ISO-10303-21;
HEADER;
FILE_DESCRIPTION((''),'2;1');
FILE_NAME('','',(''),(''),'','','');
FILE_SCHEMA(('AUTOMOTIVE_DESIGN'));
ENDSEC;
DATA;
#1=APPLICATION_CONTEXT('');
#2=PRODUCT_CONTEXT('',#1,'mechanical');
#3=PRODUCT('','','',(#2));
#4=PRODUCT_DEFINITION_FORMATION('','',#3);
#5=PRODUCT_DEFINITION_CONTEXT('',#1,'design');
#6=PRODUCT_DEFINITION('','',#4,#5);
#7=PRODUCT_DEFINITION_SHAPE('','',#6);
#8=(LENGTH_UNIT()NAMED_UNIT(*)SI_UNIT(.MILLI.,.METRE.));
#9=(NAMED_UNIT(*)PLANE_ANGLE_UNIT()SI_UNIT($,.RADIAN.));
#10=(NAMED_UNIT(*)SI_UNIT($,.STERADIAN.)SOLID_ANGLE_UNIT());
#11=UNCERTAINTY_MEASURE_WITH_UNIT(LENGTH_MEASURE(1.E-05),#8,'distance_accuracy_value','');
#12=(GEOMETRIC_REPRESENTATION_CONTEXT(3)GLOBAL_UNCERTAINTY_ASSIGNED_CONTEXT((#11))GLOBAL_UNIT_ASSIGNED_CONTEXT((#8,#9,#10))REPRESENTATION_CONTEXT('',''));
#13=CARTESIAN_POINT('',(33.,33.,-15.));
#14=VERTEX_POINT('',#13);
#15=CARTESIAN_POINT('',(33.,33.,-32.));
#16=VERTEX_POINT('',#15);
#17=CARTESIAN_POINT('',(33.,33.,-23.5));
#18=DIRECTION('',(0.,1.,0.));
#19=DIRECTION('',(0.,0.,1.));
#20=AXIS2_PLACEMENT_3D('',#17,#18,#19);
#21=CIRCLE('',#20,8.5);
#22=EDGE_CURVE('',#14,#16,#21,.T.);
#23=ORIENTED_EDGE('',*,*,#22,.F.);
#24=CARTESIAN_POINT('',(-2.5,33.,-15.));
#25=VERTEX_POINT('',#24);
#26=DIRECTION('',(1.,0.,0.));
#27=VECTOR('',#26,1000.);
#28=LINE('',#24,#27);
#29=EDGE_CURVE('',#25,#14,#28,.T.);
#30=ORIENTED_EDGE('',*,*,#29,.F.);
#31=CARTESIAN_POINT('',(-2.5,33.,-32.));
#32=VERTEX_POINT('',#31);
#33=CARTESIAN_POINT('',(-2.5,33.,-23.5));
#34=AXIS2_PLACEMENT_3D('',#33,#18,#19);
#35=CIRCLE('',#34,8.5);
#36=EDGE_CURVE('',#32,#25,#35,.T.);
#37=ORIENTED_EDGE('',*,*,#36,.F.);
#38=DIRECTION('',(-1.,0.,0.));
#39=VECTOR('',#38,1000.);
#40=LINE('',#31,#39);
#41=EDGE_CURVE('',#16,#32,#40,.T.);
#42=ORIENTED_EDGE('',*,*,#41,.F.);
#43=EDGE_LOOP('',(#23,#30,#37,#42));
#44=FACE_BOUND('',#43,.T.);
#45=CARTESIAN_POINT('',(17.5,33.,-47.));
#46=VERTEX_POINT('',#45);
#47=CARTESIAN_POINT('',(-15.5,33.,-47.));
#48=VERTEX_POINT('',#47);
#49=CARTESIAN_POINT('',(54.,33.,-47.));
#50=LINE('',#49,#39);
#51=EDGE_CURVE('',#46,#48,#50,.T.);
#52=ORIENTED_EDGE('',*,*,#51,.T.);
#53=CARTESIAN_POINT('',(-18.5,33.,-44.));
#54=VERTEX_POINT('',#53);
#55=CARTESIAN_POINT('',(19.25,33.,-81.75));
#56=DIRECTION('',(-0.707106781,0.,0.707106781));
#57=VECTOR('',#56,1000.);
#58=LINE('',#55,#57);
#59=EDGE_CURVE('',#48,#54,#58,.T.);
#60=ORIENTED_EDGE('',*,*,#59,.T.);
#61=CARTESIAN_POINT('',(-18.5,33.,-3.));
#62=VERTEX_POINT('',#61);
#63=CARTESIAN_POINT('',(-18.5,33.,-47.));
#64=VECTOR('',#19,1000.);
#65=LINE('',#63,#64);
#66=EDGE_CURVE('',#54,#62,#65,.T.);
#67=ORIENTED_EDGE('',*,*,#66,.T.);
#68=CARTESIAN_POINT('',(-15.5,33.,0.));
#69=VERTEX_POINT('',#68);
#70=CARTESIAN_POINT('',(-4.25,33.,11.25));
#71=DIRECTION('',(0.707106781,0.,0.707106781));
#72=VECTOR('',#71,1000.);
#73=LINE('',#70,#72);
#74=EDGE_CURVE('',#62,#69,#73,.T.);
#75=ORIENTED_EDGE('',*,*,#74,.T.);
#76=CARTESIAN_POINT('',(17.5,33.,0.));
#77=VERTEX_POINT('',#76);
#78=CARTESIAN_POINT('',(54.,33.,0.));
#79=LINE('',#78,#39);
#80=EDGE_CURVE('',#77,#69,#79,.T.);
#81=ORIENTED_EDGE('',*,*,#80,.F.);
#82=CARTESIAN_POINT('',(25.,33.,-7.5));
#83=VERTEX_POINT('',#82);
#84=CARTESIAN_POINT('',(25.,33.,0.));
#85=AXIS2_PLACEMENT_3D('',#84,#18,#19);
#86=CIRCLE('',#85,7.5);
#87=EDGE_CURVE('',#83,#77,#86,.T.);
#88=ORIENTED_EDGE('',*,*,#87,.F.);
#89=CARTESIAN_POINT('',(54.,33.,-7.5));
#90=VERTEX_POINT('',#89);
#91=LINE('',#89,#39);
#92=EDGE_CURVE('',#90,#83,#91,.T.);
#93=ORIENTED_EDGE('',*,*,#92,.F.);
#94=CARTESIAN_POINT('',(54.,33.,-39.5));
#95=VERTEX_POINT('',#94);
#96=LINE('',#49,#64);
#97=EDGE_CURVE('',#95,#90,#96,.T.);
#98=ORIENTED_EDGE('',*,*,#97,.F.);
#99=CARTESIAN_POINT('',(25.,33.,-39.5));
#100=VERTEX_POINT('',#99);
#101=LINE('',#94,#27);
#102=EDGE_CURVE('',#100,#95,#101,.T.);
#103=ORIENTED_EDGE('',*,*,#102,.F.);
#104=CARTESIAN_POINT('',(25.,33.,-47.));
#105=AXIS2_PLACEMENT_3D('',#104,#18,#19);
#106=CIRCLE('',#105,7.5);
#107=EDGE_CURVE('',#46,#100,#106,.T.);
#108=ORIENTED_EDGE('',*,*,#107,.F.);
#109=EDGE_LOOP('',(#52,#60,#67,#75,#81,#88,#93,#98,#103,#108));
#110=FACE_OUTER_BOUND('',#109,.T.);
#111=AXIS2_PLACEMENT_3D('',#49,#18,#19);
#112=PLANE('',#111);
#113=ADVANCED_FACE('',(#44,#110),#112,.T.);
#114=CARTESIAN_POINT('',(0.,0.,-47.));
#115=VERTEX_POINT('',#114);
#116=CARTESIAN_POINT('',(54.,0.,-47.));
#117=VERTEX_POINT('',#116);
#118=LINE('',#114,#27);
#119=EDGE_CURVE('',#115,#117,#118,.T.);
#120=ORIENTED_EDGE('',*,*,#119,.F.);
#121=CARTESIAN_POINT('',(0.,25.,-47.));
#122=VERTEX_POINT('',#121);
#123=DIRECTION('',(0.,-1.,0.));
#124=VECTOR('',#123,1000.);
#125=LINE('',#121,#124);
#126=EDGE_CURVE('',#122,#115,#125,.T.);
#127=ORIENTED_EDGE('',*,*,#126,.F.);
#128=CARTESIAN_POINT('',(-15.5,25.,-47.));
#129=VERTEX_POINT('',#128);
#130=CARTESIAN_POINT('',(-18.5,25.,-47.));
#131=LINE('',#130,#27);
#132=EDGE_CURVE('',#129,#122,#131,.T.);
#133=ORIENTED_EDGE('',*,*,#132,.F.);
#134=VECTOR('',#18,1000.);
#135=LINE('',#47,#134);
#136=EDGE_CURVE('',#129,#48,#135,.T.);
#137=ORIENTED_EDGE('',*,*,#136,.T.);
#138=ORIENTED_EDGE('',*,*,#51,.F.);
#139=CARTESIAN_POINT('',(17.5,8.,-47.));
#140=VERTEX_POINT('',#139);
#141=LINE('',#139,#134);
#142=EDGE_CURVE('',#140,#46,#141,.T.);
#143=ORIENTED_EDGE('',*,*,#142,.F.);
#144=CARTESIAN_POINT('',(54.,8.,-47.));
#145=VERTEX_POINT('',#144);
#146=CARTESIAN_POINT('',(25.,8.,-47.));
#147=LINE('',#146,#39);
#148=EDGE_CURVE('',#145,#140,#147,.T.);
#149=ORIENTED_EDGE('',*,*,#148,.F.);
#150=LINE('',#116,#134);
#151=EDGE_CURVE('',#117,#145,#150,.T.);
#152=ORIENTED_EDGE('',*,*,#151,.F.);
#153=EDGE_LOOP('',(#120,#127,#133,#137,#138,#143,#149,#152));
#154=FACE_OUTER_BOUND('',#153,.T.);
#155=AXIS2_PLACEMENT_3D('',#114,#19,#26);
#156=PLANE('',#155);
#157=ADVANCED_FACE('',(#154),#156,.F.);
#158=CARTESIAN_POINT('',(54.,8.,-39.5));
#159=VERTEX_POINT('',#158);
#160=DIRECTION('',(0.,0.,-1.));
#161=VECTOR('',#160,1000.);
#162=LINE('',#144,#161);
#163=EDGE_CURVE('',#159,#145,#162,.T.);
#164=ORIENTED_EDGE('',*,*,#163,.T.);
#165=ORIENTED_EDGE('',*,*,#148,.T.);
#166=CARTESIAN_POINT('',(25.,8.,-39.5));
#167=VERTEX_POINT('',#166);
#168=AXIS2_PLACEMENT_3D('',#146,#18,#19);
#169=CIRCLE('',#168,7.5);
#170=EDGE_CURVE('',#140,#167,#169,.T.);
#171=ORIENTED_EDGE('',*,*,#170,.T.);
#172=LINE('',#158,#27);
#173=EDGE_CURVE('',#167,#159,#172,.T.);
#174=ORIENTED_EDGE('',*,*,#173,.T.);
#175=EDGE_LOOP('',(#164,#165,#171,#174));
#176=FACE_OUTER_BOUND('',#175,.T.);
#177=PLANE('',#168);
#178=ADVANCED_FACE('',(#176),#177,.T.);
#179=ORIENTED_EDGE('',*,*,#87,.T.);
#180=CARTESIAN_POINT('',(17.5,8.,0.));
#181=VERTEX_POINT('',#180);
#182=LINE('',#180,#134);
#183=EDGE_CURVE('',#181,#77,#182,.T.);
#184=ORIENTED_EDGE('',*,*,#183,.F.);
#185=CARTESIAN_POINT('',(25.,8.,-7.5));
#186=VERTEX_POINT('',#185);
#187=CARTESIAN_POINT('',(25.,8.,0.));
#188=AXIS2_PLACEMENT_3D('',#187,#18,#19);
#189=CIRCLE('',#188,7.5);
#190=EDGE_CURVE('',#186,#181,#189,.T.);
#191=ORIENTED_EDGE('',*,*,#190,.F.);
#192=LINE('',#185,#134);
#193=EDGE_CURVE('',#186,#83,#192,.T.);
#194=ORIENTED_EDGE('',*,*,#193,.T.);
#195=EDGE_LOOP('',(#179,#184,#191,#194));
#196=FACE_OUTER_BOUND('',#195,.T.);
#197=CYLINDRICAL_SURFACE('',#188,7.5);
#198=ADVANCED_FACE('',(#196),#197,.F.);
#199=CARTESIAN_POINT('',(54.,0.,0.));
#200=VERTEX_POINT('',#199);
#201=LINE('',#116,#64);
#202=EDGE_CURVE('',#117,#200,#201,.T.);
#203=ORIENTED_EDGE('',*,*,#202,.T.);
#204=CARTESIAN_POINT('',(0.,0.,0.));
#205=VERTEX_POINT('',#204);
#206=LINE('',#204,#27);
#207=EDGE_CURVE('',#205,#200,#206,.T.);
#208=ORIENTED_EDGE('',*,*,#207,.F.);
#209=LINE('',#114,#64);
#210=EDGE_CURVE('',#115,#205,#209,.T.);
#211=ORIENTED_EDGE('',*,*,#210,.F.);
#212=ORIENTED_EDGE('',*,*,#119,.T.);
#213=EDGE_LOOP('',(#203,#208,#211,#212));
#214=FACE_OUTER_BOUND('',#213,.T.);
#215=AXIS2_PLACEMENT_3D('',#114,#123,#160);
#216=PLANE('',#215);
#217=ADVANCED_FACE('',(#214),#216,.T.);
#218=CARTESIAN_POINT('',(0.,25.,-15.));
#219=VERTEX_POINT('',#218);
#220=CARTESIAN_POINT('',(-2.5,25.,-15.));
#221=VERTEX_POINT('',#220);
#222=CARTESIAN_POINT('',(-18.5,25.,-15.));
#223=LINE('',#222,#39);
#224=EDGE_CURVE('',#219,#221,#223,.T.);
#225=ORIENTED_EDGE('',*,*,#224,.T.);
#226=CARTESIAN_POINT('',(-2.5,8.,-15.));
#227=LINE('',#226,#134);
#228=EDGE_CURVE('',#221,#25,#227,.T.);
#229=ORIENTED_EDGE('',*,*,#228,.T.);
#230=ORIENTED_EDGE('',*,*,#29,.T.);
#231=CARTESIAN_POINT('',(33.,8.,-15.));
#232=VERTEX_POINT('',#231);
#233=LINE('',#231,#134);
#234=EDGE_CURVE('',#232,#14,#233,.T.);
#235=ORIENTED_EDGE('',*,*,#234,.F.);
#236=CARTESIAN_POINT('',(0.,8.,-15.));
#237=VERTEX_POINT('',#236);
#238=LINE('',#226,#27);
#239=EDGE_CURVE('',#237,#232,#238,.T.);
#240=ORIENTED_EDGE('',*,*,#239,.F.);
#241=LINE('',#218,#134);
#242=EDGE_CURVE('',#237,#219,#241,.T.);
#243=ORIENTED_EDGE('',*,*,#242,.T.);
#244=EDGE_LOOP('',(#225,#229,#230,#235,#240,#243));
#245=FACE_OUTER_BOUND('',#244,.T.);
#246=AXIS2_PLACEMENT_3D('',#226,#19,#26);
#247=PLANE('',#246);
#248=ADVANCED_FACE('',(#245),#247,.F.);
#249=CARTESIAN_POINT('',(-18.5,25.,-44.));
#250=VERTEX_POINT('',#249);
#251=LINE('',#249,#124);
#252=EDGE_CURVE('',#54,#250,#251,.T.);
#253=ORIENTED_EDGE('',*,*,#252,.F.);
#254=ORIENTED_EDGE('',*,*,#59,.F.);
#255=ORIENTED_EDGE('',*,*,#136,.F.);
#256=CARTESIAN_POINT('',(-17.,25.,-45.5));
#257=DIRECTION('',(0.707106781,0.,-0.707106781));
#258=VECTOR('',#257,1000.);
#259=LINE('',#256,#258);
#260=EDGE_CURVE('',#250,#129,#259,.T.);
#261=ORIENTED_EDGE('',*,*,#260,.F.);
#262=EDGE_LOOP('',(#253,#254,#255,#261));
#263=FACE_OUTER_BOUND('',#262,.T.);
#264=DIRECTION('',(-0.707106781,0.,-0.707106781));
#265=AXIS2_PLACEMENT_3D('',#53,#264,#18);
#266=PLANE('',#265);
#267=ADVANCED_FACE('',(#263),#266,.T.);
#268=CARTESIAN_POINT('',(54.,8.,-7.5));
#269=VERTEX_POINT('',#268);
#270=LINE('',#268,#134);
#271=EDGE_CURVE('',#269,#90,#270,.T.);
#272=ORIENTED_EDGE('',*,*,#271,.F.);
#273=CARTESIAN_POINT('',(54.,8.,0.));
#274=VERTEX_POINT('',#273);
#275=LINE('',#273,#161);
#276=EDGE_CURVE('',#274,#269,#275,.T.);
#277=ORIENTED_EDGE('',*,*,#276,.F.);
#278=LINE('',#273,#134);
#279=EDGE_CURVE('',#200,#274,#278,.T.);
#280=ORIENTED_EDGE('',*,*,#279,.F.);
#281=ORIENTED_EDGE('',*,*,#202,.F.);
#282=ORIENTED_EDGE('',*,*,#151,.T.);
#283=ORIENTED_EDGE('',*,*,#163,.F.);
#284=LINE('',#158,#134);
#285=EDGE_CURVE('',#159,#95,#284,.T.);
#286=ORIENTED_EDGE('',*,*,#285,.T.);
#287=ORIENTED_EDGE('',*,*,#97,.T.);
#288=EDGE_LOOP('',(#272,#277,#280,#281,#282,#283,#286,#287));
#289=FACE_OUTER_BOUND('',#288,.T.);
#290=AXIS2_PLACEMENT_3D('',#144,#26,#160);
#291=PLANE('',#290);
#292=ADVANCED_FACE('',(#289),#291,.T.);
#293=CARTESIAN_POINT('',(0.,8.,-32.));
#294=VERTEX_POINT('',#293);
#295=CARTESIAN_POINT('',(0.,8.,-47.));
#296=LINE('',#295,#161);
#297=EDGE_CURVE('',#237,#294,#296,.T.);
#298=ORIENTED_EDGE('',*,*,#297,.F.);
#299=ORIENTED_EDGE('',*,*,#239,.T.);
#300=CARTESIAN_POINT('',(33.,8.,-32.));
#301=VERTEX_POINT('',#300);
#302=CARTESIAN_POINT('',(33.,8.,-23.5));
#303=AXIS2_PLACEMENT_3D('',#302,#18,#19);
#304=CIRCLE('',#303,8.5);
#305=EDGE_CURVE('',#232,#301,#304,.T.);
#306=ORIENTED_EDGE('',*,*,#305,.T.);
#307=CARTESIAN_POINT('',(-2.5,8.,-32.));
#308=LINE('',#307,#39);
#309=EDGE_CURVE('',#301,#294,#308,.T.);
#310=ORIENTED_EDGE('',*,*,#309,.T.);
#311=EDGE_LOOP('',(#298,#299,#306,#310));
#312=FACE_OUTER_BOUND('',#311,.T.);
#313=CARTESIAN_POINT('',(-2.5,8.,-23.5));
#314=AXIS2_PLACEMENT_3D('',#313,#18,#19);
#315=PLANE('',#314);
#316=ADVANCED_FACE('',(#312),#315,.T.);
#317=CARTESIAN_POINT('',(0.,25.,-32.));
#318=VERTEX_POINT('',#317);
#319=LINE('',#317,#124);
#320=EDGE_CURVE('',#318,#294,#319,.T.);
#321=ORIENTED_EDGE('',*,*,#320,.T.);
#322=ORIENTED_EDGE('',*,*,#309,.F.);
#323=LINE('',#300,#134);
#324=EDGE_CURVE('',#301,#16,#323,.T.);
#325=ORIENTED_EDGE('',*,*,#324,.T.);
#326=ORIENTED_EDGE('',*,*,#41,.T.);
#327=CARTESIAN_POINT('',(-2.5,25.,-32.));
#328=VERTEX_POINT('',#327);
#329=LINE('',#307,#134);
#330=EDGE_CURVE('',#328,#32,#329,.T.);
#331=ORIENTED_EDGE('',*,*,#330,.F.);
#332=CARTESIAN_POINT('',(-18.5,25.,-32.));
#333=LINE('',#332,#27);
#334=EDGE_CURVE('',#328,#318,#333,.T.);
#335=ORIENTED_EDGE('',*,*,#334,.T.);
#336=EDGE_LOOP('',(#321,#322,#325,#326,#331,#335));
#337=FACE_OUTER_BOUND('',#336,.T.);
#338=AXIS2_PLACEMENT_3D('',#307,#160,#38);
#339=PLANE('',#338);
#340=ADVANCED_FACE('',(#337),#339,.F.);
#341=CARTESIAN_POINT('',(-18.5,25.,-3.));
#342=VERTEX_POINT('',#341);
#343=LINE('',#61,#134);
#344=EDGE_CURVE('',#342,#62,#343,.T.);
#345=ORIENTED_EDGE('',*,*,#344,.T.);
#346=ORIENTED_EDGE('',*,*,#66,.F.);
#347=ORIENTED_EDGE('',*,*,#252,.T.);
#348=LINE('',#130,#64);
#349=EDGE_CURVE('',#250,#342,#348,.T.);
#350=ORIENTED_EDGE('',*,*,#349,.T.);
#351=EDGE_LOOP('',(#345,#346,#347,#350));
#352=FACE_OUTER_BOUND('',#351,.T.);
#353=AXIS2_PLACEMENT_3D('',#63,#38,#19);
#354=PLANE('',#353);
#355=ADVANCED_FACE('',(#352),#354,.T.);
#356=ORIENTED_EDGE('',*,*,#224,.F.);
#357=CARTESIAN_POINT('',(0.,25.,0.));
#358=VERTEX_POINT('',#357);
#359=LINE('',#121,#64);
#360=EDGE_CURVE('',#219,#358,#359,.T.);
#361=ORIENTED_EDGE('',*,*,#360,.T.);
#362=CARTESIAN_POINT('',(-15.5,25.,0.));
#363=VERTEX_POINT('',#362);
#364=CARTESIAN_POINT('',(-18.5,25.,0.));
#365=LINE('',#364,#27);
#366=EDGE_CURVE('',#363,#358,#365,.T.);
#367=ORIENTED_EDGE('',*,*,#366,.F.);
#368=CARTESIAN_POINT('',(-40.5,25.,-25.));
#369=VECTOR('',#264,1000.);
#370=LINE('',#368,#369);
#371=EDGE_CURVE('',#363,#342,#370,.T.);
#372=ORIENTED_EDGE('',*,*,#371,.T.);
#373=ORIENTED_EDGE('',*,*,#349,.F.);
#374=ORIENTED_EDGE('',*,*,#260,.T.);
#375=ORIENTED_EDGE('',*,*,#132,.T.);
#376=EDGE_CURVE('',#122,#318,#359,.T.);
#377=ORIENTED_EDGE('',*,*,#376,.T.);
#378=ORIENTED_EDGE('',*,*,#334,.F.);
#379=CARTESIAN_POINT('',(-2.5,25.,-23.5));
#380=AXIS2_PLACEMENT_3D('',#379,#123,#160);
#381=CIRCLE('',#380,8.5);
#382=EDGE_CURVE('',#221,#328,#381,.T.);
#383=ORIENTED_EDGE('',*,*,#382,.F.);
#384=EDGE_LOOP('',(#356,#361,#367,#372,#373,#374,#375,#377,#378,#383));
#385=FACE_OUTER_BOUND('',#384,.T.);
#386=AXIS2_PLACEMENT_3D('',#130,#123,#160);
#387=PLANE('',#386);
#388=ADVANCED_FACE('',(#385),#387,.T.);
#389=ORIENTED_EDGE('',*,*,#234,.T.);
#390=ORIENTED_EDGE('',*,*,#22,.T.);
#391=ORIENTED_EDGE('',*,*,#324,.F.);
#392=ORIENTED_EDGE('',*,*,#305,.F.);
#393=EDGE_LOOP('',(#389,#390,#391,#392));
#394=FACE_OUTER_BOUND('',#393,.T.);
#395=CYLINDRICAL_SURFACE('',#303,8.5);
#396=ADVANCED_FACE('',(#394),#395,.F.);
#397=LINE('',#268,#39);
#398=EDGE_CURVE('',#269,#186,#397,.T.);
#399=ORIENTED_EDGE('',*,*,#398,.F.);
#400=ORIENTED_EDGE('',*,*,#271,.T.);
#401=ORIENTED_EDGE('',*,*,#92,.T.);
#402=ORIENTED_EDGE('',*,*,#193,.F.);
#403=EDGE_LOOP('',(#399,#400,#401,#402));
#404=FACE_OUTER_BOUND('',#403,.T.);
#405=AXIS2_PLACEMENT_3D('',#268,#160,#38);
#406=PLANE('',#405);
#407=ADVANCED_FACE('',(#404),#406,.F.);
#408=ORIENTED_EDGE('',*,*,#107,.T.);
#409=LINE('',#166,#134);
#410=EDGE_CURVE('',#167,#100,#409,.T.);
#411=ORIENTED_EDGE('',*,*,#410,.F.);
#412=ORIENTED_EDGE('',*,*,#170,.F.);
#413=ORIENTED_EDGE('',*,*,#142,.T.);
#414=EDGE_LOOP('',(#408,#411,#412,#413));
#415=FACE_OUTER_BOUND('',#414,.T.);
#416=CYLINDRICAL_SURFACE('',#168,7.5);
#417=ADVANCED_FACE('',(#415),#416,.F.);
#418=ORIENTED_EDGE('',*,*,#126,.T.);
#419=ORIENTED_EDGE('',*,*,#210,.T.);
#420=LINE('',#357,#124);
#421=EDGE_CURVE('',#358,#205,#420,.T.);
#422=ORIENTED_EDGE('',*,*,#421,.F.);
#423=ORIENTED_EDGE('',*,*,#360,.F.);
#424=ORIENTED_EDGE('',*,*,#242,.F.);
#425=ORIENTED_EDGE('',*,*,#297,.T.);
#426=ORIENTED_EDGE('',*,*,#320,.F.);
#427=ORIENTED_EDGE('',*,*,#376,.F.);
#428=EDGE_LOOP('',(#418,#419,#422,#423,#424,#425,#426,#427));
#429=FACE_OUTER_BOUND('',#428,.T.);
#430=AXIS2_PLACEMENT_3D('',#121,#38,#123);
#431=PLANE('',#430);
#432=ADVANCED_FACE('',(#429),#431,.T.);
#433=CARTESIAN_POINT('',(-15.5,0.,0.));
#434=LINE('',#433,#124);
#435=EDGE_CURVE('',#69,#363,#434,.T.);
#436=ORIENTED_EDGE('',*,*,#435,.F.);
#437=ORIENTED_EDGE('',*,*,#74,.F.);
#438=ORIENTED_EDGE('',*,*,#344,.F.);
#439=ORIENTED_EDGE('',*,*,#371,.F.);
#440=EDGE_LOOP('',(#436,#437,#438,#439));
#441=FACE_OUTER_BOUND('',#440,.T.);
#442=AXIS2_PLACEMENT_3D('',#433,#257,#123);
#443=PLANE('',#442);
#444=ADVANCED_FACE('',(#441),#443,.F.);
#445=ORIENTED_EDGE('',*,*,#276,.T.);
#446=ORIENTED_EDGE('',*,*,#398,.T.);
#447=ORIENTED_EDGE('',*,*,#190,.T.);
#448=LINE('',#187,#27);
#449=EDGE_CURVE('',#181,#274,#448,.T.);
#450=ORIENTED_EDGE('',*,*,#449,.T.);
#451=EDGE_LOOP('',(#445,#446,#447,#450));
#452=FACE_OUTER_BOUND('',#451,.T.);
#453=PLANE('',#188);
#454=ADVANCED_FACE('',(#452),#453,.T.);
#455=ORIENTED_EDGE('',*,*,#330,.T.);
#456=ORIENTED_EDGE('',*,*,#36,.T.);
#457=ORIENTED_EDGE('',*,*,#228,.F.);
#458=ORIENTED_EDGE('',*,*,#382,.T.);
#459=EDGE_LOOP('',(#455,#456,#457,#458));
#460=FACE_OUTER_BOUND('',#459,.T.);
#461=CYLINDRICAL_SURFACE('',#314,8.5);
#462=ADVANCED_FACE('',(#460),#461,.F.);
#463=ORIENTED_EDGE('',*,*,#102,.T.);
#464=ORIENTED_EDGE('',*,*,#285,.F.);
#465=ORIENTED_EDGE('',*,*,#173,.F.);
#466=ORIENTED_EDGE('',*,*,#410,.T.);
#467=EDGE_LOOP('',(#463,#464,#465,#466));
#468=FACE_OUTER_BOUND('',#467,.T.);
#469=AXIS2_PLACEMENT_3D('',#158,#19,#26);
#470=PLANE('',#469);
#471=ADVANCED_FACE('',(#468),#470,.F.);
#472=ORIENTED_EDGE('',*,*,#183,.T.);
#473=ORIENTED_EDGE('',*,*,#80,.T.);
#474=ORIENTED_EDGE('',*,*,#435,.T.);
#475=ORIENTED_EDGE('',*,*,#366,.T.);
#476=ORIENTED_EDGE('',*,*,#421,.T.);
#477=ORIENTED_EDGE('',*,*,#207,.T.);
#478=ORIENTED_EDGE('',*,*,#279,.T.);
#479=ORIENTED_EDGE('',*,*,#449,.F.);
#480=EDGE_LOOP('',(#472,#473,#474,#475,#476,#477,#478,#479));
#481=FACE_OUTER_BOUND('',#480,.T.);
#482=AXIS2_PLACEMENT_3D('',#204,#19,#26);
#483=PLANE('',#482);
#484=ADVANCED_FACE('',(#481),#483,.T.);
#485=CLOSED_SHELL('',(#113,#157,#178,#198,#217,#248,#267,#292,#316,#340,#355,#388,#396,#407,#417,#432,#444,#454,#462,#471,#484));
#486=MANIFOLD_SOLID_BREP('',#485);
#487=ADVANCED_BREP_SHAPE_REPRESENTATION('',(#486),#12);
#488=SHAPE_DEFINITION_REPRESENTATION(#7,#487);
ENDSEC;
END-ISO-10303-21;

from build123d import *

# Parameters (mm, degrees)
BASE_BLOCK_DEPTH       = 47
SIDE_NOTCH_A_DEPTH     = 25
SIDE_NOTCH_B_DEPTH     = 25
GUIDE_SLOT_DEPTH       = 25
EDGE_CHAMFER_3X45_SIZE = 3


with BuildPart() as part:
    # Base Profile Sketch → Base Block (new body)
    with BuildSketch(Plane.XY):
        Polygon((0, 0), (54, 0), (54, 8), (54, 33), (-18.5, 33), (-18.5, 25), (0, 25), align=None)
    extrude(amount=-BASE_BLOCK_DEPTH)

    # Side Notch A Sketch → Side Notch A (cut)
    with BuildSketch(Plane(origin=(0, 33, 0), x_dir=(1, 0, 0), z_dir=(0, 1, 0))):
        with BuildLine():
            Line((54, 0), (54, 7.5))
            Line((54, 7.5), (25, 7.5))
            ThreePointArc((25, 7.5), (19.696699141, 5.303300859), (17.5, 0))
            Line((17.5, 0), (25, 0))
            Line((25, 0), (54, 0))
        make_face()
    extrude(amount=-SIDE_NOTCH_A_DEPTH, mode=Mode.SUBTRACT)

    # Side Notch B Sketch → Side Notch B (cut)
    with BuildSketch(Plane(origin=(0, 33, 0), x_dir=(1, 0, 0), z_dir=(0, 1, 0))):
        with BuildLine():
            Line((54, 47), (54, 39.5))
            Line((54, 39.5), (25, 39.5))
            ThreePointArc((25, 39.5), (19.696699141, 41.696699141), (17.5, 47))
            Line((17.5, 47), (25, 47))
            Line((25, 47), (54, 47))
        make_face()
    extrude(amount=-SIDE_NOTCH_B_DEPTH, mode=Mode.SUBTRACT)

    # Guide Slot Sketch → Guide Slot (cut)
    with BuildSketch(Plane(origin=(0, 33, 0), x_dir=(1, 0, 0), z_dir=(0, 1, 0))):
        with BuildLine():
            Line((-2.5, 32), (33, 32))
            ThreePointArc((33, 32), (41.5, 23.5), (33, 15))
            Line((33, 15), (-2.5, 15))
            ThreePointArc((-2.5, 15), (-11, 23.5), (-2.5, 32))
        make_face()
    extrude(amount=-GUIDE_SLOT_DEPTH, mode=Mode.SUBTRACT)

    # Edge Chamfer 3x45
    edge_chamfer_3x45_edges = [part.edges().sort_by_distance(p)[0] for p in [
        (-18.5, 29, -47),
        (-18.5, 29, 0),
    ]]
    chamfer(edge_chamfer_3x45_edges, length=EDGE_CHAMFER_3X45_SIZE)


solid = part.part
